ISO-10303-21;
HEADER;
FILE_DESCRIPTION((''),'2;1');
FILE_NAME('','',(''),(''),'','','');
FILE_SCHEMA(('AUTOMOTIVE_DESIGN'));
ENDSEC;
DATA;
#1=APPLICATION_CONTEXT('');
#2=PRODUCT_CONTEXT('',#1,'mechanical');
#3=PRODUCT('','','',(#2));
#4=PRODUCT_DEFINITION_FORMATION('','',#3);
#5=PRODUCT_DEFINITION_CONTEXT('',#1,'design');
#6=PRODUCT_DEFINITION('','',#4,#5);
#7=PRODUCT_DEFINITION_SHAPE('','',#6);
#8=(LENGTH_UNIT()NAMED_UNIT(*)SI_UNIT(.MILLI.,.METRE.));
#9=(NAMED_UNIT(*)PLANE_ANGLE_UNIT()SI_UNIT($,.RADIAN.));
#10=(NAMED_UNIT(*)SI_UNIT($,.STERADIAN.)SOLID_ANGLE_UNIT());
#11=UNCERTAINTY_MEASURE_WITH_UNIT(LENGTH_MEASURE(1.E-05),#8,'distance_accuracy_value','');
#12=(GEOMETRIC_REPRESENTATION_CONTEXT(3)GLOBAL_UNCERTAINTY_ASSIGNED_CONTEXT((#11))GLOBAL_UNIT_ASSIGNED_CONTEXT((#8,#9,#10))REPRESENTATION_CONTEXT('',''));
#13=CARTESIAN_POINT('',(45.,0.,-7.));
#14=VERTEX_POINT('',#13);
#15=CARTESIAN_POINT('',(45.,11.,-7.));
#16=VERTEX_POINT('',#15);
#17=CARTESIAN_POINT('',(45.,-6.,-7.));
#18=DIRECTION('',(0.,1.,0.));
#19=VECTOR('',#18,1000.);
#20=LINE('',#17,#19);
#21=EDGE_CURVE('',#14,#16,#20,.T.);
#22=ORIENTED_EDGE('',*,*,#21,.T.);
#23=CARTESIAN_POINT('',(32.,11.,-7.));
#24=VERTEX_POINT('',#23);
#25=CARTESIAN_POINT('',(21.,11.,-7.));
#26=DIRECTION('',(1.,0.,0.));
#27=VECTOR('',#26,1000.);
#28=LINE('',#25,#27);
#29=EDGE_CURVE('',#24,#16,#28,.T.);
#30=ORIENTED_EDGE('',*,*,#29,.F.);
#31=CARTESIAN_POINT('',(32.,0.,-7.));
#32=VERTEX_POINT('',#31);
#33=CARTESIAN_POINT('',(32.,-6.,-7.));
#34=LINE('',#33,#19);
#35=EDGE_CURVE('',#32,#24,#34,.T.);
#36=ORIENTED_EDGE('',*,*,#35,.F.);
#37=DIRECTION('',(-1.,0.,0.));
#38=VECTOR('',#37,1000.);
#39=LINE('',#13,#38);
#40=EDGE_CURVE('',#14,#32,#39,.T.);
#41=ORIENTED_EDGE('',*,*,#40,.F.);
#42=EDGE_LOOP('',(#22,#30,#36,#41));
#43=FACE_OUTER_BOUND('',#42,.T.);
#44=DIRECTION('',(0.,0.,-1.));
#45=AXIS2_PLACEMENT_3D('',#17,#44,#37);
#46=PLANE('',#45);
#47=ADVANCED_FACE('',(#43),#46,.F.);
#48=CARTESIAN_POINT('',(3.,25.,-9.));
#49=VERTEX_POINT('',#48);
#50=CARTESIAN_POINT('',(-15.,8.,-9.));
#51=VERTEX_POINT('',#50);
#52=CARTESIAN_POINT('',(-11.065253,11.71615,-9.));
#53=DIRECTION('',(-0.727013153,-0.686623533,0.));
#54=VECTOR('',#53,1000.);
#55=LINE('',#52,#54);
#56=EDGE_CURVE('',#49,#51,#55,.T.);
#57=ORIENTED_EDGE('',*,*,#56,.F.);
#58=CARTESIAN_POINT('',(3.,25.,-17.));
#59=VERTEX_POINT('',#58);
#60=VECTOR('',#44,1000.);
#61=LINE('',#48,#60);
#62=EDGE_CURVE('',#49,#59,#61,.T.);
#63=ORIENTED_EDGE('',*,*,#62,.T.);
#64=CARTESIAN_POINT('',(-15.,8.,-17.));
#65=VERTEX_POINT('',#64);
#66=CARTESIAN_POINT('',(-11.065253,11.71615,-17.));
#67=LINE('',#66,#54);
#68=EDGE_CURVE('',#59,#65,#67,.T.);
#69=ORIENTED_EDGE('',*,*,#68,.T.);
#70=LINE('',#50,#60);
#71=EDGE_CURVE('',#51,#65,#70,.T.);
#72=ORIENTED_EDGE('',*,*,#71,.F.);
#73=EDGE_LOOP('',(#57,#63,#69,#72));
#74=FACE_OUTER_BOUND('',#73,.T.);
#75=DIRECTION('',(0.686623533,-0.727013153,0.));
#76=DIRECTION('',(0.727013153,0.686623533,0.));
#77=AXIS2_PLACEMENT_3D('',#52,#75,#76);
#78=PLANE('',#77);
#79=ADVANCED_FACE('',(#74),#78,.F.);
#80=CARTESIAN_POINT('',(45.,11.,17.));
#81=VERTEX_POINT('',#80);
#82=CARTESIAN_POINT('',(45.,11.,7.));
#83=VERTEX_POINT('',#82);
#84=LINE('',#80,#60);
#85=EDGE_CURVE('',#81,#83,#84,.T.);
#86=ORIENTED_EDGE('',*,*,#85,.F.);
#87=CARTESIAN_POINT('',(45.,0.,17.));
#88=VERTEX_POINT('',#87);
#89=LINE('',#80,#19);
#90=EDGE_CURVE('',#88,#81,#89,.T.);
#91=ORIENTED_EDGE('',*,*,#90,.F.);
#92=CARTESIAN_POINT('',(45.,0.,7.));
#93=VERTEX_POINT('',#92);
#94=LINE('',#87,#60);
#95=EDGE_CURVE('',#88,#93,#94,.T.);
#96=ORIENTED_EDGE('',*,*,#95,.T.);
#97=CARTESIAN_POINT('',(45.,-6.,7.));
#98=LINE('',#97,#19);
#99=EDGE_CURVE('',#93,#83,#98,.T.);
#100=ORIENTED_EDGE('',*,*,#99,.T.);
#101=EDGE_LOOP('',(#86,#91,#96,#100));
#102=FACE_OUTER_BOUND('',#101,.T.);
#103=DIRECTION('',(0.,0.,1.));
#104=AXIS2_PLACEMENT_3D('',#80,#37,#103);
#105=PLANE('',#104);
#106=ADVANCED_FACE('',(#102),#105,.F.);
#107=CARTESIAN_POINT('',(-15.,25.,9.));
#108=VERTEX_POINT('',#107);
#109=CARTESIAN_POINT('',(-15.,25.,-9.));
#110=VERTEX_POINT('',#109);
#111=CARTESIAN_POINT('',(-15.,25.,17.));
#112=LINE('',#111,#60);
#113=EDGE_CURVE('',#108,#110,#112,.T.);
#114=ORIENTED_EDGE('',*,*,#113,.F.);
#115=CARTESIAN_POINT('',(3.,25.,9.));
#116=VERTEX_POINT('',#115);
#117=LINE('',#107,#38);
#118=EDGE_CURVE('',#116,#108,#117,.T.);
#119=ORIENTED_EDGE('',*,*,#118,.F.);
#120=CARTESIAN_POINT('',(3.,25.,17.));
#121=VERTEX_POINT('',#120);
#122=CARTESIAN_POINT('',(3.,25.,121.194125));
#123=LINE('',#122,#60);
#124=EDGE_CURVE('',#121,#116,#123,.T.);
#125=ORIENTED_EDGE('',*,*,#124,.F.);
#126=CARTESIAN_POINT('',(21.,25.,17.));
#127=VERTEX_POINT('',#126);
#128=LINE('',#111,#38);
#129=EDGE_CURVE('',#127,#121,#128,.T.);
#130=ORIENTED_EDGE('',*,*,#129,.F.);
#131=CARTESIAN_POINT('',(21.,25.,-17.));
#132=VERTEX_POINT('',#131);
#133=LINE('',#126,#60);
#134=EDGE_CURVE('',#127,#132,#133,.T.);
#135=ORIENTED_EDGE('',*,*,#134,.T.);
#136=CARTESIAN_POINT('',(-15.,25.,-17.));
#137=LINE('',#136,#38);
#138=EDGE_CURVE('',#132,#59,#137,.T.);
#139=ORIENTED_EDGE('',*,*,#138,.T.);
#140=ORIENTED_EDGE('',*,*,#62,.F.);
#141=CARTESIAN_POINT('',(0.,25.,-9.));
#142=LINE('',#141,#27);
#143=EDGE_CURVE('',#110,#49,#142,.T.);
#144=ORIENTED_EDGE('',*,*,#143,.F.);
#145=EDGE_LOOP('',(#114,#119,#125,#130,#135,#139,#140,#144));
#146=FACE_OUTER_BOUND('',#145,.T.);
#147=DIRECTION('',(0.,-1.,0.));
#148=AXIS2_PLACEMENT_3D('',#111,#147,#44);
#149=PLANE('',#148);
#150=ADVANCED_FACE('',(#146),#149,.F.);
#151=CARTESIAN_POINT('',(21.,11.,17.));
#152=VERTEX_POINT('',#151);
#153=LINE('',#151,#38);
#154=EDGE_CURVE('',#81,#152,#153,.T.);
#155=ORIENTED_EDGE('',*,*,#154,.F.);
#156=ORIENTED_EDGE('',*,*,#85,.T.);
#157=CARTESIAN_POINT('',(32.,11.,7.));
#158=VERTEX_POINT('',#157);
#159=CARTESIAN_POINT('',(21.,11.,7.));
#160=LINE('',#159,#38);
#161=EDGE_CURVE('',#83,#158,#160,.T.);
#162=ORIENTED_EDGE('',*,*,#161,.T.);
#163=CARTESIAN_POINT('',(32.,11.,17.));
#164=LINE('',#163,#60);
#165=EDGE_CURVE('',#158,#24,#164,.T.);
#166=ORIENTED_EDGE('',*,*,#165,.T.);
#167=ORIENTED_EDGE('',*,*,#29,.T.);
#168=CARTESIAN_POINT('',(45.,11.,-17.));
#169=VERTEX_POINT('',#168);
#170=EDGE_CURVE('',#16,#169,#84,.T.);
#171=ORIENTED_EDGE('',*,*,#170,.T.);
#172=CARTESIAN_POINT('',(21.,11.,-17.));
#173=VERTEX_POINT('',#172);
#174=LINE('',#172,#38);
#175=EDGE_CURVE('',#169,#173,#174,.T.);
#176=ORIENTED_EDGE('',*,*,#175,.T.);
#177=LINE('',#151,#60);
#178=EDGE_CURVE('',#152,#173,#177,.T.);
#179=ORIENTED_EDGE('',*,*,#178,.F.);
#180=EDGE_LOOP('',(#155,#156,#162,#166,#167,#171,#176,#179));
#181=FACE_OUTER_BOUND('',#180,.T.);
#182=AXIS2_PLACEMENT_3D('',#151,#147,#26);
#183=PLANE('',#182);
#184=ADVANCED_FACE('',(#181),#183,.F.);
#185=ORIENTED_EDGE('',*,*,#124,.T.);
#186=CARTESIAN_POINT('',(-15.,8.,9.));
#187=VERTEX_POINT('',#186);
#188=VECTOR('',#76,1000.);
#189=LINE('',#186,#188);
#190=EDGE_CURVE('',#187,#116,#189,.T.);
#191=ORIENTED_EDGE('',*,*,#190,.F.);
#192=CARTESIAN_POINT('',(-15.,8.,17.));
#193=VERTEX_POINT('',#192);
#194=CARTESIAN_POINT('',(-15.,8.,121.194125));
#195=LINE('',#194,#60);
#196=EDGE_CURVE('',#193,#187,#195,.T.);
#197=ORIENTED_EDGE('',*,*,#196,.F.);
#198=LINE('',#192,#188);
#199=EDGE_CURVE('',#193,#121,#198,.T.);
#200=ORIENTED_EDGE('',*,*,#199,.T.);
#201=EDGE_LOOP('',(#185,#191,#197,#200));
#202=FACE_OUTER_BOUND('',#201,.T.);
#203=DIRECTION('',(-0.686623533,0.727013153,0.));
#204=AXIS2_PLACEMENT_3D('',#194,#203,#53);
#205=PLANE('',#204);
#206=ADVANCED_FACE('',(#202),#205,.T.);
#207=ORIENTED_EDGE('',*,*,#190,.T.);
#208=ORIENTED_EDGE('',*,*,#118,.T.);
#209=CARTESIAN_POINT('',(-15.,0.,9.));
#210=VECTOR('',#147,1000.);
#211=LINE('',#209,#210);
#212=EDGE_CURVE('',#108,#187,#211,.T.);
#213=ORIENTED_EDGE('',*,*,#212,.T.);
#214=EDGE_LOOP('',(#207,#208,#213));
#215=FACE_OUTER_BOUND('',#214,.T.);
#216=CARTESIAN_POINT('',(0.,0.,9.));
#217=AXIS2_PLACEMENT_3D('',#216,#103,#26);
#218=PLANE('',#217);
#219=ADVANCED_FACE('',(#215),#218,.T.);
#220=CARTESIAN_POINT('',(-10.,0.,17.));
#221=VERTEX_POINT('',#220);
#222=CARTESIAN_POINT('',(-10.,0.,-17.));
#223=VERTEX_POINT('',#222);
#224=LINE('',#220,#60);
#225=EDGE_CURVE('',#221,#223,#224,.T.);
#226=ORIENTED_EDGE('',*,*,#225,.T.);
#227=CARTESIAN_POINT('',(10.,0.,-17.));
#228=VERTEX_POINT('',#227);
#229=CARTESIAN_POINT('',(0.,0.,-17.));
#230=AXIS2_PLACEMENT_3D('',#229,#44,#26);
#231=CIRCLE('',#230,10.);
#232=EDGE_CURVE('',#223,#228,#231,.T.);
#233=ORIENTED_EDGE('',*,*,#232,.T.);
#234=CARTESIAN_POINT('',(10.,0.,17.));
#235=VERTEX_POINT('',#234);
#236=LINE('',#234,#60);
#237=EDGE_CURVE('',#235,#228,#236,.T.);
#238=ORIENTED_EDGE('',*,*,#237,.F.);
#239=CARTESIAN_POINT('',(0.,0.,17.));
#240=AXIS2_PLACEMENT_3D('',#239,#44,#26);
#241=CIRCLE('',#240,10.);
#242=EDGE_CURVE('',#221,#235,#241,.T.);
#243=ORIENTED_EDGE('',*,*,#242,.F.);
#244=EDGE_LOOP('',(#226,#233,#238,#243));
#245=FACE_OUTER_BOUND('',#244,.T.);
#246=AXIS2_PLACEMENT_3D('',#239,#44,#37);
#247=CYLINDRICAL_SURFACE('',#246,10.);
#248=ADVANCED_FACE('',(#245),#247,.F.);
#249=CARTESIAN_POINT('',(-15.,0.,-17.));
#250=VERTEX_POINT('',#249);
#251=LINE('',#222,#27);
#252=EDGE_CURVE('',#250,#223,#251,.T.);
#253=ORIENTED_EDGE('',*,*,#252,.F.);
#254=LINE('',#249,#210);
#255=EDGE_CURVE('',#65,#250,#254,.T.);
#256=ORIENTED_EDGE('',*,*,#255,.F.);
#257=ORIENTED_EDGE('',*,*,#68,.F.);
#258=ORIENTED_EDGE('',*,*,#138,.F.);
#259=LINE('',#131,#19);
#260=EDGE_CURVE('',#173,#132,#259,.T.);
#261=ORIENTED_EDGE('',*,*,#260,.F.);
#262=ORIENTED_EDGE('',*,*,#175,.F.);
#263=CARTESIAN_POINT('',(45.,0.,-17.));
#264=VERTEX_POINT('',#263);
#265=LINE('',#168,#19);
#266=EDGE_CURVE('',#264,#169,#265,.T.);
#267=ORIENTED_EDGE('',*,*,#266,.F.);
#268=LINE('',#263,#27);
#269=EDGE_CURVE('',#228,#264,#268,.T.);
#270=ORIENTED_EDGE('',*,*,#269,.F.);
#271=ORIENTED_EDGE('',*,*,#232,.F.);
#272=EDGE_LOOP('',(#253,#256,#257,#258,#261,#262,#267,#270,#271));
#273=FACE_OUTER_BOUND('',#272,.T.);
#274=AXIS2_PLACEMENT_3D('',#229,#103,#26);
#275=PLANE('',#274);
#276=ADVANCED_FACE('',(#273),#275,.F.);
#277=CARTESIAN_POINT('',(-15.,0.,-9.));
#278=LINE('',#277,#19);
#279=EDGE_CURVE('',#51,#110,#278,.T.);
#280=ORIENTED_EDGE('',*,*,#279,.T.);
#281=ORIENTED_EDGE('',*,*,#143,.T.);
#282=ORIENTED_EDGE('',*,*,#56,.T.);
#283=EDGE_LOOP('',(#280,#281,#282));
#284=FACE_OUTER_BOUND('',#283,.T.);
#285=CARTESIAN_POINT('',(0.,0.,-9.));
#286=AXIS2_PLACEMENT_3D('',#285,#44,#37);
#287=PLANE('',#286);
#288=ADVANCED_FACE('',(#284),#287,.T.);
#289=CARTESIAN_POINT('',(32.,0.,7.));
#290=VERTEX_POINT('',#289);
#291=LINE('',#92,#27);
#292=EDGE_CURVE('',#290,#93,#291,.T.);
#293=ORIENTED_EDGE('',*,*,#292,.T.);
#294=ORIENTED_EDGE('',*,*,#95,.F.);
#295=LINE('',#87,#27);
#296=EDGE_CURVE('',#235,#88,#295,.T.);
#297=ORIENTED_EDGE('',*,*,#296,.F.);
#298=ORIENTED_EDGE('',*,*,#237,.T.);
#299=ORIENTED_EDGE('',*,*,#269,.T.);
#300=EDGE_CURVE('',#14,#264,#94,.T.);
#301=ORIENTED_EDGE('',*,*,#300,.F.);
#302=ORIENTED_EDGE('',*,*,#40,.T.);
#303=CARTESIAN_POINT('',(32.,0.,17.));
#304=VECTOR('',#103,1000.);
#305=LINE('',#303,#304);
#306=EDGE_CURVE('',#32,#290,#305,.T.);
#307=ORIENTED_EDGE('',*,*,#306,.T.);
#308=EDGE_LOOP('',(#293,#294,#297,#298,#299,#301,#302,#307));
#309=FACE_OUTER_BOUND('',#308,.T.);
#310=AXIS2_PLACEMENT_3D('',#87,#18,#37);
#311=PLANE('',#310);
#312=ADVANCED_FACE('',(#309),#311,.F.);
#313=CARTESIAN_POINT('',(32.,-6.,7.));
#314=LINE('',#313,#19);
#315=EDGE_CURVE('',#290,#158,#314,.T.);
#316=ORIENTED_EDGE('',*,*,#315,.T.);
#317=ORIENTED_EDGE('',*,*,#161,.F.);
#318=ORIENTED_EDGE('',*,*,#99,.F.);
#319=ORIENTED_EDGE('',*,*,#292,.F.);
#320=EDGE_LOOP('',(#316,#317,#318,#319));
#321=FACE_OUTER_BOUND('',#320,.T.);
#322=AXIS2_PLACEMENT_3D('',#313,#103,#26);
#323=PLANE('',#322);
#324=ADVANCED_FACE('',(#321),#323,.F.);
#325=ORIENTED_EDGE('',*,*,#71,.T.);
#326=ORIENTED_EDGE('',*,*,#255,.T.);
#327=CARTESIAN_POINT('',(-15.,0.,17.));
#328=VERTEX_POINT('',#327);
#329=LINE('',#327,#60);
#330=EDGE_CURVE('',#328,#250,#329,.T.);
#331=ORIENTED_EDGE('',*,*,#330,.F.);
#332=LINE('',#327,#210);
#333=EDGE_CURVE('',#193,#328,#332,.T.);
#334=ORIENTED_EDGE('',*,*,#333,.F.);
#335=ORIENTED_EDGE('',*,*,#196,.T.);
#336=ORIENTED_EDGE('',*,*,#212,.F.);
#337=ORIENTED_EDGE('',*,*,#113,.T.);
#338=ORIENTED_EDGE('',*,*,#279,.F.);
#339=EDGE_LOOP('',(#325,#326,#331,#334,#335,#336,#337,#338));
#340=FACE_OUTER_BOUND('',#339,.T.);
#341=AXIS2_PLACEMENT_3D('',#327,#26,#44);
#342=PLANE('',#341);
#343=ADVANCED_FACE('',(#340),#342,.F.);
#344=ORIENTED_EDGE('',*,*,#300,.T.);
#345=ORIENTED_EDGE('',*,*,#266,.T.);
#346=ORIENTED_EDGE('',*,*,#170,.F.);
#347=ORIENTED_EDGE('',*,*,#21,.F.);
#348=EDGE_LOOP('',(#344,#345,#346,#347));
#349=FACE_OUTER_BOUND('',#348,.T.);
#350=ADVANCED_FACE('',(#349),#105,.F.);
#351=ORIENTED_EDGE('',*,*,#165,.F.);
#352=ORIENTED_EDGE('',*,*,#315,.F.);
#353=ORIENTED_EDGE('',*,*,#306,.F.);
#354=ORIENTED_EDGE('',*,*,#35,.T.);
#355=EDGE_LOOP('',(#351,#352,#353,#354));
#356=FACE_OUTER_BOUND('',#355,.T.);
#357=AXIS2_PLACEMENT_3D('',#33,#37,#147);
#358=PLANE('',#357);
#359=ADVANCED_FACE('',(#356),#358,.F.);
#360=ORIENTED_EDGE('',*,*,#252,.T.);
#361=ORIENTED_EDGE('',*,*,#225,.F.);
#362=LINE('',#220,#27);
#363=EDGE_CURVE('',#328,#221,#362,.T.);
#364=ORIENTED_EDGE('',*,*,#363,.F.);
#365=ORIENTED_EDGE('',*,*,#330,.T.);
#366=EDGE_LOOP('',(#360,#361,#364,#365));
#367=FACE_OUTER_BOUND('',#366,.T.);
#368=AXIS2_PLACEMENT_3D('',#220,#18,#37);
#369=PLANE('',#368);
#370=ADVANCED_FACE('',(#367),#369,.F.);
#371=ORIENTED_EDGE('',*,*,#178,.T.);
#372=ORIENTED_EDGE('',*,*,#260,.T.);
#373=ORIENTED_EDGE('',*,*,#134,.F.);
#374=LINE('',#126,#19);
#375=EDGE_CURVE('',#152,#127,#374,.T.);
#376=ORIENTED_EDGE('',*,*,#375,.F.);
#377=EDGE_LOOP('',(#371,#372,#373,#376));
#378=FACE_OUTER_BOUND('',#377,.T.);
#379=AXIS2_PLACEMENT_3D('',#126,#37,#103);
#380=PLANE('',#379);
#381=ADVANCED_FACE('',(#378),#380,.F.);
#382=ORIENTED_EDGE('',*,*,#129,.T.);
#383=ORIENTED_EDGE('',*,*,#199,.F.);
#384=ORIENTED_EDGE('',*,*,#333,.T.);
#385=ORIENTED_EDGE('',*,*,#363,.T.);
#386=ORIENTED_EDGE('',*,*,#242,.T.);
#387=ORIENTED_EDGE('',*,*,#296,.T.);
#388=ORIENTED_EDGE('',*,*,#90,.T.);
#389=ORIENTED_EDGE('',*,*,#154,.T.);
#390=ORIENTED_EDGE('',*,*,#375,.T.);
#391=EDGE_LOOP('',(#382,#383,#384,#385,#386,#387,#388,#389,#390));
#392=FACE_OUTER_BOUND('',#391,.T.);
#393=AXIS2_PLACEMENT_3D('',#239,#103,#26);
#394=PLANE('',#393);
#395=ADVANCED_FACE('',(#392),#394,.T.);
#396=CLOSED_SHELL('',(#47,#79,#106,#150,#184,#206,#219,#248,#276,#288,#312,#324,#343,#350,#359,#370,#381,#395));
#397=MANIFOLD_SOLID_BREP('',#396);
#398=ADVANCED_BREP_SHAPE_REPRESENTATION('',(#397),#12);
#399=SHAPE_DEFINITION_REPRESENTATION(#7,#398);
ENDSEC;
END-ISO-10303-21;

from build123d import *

# Parameters (mm, degrees)
BASE_BLOCK_DEPTH               = 17
END_SLOT_SKETCH_W              = 13
END_SLOT_SKETCH_H              = 14
END_SLOT_14X13_DEPTH           = 17
HALF_ROUND_NOTCH_R8_DEPTH      = 62.692787261
HALF_ROUND_NOTCH_R8_DEPTH_BACK = 8
SIDE_PROFILE_CUT_DEPTH         = 8


with BuildPart() as part:
    # Base Block Profile → Base Block (new, symmetric)
    with BuildSketch(Plane.XY):
        with BuildLine():
            Line((-15, 0), (-15, 25))
            Line((-15, 25), (21, 25))
            Line((21, 25), (21, 11))
            Line((21, 11), (45, 11))
            Line((45, 11), (45, 0))
            Line((45, 0), (10, 0))
            ThreePointArc((10, 0), (0, 10), (-10, 0))
            Line((-10, 0), (-15, 0))
        make_face()
    extrude(amount=BASE_BLOCK_DEPTH, both=True)

    # End Slot Sketch → End Slot 14x13 (cut, symmetric)
    with BuildSketch(Plane(origin=(0, 11, 0), x_dir=(1, 0, 0), z_dir=(0, 1, 0))):
        with Locations((38.5, 0)):
            Rectangle(END_SLOT_SKETCH_W, END_SLOT_SKETCH_H)
    extrude(amount=END_SLOT_14X13_DEPTH, both=True, mode=Mode.SUBTRACT)

    # Half-Round Notch Sketch → Half-Round Notch R8 (cut, two sides: drawn at the far end of the back side and taken through both)
    with BuildSketch(Plane.XY.offset(17).offset(-HALF_ROUND_NOTCH_R8_DEPTH_BACK)):
        Polygon((-112.94589795, -84.504459175), (-15, 8), (3, 25), (100.94589795, 117.504459175), (-84.0630204, 313.396255074), (-297.9548163, 111.387336725), align=None)
    extrude(amount=HALF_ROUND_NOTCH_R8_DEPTH + HALF_ROUND_NOTCH_R8_DEPTH_BACK, mode=Mode.SUBTRACT)

    # Side Profile Cut Sketch → Side Profile Cut (cut)
    with BuildSketch(Plane(origin=(0, 0, -17), x_dir=(-1, 0, 0), z_dir=(0, 0, -1))):
        Polygon((15, 25), (-3, 25), (15, 8), align=None)
    extrude(amount=-SIDE_PROFILE_CUT_DEPTH, mode=Mode.SUBTRACT)


solid = part.part
